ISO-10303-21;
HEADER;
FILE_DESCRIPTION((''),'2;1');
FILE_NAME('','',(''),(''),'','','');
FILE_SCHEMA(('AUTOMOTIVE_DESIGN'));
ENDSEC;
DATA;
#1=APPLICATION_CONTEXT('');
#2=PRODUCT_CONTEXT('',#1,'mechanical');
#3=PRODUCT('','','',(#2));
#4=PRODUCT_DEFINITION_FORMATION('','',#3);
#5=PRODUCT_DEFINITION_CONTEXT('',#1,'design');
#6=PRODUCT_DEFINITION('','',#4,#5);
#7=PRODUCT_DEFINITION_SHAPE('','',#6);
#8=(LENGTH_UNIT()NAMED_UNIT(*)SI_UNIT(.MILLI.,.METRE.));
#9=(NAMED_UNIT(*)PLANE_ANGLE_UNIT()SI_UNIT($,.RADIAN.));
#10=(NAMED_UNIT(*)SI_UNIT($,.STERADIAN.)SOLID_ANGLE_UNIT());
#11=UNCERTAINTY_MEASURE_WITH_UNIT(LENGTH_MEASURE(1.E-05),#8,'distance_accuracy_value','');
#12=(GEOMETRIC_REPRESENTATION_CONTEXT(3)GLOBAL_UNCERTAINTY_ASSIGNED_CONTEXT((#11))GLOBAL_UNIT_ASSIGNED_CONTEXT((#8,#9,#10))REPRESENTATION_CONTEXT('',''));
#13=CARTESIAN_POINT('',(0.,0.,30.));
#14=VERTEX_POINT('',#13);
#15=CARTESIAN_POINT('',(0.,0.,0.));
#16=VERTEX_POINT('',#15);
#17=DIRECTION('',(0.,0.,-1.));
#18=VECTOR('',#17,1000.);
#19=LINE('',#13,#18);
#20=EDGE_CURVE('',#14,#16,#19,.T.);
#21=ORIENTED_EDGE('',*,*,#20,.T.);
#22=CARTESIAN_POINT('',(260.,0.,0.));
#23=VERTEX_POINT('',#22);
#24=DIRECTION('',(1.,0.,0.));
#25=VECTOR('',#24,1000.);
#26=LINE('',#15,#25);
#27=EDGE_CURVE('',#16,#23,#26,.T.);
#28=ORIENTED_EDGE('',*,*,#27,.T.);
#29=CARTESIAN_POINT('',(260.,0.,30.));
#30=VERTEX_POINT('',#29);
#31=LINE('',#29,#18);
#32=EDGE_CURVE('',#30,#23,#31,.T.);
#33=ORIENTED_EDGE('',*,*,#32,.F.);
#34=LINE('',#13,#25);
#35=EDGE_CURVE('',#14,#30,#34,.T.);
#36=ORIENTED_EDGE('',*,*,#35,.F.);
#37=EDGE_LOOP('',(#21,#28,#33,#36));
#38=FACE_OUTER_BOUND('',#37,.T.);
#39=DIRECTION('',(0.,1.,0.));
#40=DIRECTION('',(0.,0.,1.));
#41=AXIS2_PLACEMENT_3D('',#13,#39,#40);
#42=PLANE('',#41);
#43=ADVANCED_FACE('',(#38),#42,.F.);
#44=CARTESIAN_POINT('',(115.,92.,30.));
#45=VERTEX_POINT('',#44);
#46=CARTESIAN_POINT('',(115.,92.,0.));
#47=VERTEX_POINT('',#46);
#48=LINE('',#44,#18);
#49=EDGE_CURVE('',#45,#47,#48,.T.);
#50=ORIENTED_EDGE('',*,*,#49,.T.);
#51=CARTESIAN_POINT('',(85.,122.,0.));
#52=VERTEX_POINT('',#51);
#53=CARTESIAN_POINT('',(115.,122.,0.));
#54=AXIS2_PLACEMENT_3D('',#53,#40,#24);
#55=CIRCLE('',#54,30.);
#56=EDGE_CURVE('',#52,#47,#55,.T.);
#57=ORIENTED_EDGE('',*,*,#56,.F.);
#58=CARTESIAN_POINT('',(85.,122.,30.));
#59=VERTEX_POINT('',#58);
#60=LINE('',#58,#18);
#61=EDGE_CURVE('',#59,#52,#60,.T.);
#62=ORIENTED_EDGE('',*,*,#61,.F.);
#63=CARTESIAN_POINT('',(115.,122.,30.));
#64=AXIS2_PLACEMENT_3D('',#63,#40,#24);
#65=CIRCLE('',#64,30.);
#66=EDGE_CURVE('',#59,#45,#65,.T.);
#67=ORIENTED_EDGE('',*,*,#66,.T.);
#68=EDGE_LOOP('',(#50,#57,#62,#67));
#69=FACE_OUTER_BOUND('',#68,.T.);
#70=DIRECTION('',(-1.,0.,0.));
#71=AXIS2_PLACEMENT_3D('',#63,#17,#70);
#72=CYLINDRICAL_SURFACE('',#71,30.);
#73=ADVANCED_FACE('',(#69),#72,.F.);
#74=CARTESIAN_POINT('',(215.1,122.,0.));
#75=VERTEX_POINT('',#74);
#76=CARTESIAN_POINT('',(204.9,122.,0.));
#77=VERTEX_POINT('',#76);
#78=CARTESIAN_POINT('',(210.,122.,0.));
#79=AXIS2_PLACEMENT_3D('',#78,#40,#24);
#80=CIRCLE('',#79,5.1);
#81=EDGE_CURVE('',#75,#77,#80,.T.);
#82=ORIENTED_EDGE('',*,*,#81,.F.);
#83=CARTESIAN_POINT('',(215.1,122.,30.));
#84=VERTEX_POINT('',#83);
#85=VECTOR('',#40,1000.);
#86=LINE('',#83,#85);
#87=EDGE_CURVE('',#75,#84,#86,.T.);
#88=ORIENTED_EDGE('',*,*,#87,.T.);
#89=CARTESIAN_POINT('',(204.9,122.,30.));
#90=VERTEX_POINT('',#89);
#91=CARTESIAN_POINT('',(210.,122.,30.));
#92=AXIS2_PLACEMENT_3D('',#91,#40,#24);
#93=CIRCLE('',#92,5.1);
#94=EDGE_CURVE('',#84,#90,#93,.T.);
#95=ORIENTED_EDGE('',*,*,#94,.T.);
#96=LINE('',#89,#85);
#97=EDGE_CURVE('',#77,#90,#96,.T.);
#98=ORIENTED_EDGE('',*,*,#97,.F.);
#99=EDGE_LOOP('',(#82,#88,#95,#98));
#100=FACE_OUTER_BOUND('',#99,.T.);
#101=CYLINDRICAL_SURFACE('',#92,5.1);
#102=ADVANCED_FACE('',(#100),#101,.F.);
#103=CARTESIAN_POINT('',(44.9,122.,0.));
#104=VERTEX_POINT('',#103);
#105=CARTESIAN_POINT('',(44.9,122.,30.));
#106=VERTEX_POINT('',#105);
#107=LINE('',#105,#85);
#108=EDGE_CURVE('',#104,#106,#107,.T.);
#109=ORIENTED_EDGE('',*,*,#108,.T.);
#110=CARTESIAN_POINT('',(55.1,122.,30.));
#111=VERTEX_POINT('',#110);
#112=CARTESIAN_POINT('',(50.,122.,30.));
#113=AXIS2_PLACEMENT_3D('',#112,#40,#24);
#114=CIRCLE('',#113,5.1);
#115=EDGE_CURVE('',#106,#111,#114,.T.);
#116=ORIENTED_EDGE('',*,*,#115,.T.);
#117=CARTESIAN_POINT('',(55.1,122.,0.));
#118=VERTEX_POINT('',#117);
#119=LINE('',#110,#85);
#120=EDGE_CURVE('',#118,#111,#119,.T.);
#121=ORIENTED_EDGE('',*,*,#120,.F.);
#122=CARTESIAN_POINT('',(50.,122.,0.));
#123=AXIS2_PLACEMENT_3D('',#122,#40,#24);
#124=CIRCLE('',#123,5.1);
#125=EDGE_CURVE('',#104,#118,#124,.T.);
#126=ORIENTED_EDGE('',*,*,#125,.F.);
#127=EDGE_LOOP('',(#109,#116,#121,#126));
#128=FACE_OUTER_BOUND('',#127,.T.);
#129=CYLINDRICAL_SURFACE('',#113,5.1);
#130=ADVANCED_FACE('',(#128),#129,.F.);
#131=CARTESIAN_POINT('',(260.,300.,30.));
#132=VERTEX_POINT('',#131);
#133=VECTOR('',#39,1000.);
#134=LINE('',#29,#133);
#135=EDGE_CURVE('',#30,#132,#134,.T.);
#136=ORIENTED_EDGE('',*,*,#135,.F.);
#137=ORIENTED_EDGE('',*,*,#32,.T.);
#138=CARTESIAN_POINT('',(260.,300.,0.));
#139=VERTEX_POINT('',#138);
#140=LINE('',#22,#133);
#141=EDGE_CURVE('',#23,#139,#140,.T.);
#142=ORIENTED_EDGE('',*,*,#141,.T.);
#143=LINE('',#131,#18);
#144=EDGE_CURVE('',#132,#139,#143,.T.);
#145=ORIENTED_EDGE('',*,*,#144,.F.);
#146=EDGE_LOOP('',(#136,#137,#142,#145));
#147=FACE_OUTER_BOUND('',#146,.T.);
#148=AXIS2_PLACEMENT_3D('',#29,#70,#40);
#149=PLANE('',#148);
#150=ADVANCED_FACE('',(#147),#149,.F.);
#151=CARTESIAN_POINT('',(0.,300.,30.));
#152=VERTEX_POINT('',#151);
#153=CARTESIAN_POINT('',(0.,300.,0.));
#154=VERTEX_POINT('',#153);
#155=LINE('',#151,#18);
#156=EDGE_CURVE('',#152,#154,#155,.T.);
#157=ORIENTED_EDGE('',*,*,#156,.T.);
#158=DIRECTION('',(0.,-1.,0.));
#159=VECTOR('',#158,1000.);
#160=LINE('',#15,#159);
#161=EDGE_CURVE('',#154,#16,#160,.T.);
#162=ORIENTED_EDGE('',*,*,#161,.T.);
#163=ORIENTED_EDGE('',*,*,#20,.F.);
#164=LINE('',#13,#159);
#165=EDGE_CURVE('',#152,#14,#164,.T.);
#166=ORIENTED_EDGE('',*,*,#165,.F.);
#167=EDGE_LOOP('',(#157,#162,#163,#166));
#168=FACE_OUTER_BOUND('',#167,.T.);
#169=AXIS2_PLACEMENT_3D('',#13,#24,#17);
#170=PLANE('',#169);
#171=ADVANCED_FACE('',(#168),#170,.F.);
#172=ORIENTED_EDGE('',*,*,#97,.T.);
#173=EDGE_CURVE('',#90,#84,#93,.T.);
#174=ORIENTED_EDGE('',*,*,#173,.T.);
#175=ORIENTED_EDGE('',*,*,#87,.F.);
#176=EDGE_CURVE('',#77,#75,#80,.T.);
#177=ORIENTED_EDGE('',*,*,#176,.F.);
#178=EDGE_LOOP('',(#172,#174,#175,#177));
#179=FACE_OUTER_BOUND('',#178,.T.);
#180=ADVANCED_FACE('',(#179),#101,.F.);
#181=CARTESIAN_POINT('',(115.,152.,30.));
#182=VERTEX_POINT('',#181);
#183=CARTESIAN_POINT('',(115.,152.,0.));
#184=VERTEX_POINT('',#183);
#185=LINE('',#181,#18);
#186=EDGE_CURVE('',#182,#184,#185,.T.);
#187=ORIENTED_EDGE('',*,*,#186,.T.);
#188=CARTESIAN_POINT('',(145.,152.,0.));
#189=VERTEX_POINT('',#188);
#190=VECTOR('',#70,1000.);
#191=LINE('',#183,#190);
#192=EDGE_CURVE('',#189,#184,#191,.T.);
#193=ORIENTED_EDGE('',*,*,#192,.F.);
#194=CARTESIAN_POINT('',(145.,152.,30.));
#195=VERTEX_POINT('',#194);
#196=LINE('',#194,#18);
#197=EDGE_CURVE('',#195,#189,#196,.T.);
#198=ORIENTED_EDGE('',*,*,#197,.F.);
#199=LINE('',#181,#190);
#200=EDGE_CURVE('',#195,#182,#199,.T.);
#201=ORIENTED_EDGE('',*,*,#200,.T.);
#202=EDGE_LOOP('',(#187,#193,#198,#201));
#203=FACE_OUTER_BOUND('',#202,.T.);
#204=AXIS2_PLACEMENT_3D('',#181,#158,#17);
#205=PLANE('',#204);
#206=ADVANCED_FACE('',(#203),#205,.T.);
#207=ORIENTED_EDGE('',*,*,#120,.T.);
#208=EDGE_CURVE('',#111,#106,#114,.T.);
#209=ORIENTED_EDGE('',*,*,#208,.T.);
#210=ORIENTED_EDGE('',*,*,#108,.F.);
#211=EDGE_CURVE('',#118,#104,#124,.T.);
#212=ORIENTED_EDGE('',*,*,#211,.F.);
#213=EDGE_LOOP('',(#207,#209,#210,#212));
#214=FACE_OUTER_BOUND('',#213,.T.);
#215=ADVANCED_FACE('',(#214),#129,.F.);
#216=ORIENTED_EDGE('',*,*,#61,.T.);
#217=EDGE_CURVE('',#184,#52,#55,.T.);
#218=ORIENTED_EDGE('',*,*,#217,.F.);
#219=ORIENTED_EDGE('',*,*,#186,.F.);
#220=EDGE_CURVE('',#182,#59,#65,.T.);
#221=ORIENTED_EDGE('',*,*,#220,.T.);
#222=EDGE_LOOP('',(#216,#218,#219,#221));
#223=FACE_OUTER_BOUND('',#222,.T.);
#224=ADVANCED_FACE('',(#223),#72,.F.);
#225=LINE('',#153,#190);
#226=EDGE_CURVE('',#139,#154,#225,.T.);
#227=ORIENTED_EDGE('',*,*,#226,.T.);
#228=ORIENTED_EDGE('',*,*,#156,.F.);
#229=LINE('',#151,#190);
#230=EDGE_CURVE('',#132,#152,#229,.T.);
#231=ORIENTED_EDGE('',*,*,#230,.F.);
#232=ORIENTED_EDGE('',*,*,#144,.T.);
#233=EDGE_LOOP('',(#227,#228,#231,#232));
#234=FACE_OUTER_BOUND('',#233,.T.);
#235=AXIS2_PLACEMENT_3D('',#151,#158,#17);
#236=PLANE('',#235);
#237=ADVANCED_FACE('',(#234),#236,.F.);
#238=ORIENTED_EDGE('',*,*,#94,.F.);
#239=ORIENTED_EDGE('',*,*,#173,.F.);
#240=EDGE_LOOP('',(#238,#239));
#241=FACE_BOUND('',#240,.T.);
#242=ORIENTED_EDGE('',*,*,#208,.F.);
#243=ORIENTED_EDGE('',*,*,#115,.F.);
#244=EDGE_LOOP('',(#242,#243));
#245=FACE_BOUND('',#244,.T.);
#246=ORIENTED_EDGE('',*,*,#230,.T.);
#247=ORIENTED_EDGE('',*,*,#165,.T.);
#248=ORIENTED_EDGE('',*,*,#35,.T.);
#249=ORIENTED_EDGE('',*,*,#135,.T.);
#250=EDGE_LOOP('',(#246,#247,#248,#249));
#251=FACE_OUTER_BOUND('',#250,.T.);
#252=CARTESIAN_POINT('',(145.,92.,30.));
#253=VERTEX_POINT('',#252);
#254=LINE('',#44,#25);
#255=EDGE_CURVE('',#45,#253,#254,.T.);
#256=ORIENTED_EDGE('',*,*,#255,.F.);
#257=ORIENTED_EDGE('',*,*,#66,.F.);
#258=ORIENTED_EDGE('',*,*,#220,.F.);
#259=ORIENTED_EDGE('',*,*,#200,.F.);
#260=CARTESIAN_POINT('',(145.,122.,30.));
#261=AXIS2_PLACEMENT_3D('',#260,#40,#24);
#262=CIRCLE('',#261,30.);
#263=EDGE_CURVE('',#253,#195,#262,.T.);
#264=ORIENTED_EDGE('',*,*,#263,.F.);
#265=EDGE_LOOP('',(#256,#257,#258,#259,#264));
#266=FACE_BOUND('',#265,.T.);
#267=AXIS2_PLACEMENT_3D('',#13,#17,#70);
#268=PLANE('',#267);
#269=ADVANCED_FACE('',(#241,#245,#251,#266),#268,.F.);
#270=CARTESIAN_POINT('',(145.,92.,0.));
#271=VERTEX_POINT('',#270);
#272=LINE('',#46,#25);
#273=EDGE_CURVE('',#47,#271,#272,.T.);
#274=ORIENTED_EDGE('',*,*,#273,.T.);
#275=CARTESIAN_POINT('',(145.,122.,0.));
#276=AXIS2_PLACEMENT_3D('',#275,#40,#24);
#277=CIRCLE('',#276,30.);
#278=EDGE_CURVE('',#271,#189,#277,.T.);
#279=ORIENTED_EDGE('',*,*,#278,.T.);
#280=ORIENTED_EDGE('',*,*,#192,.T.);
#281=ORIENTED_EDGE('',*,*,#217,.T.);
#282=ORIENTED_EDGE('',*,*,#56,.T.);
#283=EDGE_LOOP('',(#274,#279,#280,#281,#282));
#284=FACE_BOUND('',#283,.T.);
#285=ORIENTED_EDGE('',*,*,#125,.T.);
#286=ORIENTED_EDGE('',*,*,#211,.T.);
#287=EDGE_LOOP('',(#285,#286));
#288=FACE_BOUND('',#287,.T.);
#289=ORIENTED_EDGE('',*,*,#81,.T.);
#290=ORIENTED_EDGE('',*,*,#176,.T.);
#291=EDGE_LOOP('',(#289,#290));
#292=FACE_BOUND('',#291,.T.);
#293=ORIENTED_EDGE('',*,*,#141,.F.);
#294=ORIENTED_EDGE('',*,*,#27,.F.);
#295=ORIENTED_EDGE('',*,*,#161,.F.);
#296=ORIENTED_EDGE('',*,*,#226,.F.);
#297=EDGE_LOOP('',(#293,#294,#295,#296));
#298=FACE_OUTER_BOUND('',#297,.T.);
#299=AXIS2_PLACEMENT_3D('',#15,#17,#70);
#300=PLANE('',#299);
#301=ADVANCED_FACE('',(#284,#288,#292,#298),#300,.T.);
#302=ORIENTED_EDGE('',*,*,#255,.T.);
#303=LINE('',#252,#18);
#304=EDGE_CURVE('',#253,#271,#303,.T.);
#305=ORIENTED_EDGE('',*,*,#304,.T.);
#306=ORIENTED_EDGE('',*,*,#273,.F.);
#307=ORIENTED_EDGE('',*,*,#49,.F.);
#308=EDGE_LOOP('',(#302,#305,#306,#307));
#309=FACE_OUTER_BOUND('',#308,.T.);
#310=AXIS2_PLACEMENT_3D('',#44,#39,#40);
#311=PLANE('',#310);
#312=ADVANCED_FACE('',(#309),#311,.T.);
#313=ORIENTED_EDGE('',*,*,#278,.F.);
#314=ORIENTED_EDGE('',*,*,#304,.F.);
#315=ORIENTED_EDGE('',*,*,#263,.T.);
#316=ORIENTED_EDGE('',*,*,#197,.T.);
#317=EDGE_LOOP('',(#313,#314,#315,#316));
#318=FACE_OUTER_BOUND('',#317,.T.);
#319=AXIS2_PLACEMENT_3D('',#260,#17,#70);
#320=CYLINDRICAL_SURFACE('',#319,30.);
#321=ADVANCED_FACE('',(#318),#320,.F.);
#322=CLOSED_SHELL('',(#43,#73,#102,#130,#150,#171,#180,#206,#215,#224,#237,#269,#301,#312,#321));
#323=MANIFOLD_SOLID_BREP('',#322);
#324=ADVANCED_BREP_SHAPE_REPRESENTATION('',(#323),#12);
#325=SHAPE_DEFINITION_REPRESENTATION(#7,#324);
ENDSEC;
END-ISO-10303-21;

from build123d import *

# Parameters (mm, degrees)
SKETCH1_W            = 260
SKETCH1_H            = 300
BOSS_EXTRUDE1_DEPTH  = 30
M12_THREADED_HOLE1_D = 10.2


with BuildPart() as part:
    # Sketch1 → Boss-Extrude1 (new body)
    with BuildSketch(Plane.XY):
        with Locations((130, 150)):
            Rectangle(SKETCH1_W, SKETCH1_H)
        with BuildLine():
            Line((115, 152), (145, 152))
            ThreePointArc((145, 152), (175, 122), (145, 92))
            Line((145, 92), (115, 92))
            ThreePointArc((115, 92), (85, 122), (115, 152))
        make_face(mode=Mode.SUBTRACT)
    extrude(amount=BOSS_EXTRUDE1_DEPTH)

    # M12 Threaded hole1 (through all)
    with Locations(Plane(origin=(50, 122, 30), x_dir=(1, 0, 0), z_dir=(0, 0, 1))):
        with Locations((0, 0), (160, 0)):
            Hole(M12_THREADED_HOLE1_D / 2)


solid = part.part
